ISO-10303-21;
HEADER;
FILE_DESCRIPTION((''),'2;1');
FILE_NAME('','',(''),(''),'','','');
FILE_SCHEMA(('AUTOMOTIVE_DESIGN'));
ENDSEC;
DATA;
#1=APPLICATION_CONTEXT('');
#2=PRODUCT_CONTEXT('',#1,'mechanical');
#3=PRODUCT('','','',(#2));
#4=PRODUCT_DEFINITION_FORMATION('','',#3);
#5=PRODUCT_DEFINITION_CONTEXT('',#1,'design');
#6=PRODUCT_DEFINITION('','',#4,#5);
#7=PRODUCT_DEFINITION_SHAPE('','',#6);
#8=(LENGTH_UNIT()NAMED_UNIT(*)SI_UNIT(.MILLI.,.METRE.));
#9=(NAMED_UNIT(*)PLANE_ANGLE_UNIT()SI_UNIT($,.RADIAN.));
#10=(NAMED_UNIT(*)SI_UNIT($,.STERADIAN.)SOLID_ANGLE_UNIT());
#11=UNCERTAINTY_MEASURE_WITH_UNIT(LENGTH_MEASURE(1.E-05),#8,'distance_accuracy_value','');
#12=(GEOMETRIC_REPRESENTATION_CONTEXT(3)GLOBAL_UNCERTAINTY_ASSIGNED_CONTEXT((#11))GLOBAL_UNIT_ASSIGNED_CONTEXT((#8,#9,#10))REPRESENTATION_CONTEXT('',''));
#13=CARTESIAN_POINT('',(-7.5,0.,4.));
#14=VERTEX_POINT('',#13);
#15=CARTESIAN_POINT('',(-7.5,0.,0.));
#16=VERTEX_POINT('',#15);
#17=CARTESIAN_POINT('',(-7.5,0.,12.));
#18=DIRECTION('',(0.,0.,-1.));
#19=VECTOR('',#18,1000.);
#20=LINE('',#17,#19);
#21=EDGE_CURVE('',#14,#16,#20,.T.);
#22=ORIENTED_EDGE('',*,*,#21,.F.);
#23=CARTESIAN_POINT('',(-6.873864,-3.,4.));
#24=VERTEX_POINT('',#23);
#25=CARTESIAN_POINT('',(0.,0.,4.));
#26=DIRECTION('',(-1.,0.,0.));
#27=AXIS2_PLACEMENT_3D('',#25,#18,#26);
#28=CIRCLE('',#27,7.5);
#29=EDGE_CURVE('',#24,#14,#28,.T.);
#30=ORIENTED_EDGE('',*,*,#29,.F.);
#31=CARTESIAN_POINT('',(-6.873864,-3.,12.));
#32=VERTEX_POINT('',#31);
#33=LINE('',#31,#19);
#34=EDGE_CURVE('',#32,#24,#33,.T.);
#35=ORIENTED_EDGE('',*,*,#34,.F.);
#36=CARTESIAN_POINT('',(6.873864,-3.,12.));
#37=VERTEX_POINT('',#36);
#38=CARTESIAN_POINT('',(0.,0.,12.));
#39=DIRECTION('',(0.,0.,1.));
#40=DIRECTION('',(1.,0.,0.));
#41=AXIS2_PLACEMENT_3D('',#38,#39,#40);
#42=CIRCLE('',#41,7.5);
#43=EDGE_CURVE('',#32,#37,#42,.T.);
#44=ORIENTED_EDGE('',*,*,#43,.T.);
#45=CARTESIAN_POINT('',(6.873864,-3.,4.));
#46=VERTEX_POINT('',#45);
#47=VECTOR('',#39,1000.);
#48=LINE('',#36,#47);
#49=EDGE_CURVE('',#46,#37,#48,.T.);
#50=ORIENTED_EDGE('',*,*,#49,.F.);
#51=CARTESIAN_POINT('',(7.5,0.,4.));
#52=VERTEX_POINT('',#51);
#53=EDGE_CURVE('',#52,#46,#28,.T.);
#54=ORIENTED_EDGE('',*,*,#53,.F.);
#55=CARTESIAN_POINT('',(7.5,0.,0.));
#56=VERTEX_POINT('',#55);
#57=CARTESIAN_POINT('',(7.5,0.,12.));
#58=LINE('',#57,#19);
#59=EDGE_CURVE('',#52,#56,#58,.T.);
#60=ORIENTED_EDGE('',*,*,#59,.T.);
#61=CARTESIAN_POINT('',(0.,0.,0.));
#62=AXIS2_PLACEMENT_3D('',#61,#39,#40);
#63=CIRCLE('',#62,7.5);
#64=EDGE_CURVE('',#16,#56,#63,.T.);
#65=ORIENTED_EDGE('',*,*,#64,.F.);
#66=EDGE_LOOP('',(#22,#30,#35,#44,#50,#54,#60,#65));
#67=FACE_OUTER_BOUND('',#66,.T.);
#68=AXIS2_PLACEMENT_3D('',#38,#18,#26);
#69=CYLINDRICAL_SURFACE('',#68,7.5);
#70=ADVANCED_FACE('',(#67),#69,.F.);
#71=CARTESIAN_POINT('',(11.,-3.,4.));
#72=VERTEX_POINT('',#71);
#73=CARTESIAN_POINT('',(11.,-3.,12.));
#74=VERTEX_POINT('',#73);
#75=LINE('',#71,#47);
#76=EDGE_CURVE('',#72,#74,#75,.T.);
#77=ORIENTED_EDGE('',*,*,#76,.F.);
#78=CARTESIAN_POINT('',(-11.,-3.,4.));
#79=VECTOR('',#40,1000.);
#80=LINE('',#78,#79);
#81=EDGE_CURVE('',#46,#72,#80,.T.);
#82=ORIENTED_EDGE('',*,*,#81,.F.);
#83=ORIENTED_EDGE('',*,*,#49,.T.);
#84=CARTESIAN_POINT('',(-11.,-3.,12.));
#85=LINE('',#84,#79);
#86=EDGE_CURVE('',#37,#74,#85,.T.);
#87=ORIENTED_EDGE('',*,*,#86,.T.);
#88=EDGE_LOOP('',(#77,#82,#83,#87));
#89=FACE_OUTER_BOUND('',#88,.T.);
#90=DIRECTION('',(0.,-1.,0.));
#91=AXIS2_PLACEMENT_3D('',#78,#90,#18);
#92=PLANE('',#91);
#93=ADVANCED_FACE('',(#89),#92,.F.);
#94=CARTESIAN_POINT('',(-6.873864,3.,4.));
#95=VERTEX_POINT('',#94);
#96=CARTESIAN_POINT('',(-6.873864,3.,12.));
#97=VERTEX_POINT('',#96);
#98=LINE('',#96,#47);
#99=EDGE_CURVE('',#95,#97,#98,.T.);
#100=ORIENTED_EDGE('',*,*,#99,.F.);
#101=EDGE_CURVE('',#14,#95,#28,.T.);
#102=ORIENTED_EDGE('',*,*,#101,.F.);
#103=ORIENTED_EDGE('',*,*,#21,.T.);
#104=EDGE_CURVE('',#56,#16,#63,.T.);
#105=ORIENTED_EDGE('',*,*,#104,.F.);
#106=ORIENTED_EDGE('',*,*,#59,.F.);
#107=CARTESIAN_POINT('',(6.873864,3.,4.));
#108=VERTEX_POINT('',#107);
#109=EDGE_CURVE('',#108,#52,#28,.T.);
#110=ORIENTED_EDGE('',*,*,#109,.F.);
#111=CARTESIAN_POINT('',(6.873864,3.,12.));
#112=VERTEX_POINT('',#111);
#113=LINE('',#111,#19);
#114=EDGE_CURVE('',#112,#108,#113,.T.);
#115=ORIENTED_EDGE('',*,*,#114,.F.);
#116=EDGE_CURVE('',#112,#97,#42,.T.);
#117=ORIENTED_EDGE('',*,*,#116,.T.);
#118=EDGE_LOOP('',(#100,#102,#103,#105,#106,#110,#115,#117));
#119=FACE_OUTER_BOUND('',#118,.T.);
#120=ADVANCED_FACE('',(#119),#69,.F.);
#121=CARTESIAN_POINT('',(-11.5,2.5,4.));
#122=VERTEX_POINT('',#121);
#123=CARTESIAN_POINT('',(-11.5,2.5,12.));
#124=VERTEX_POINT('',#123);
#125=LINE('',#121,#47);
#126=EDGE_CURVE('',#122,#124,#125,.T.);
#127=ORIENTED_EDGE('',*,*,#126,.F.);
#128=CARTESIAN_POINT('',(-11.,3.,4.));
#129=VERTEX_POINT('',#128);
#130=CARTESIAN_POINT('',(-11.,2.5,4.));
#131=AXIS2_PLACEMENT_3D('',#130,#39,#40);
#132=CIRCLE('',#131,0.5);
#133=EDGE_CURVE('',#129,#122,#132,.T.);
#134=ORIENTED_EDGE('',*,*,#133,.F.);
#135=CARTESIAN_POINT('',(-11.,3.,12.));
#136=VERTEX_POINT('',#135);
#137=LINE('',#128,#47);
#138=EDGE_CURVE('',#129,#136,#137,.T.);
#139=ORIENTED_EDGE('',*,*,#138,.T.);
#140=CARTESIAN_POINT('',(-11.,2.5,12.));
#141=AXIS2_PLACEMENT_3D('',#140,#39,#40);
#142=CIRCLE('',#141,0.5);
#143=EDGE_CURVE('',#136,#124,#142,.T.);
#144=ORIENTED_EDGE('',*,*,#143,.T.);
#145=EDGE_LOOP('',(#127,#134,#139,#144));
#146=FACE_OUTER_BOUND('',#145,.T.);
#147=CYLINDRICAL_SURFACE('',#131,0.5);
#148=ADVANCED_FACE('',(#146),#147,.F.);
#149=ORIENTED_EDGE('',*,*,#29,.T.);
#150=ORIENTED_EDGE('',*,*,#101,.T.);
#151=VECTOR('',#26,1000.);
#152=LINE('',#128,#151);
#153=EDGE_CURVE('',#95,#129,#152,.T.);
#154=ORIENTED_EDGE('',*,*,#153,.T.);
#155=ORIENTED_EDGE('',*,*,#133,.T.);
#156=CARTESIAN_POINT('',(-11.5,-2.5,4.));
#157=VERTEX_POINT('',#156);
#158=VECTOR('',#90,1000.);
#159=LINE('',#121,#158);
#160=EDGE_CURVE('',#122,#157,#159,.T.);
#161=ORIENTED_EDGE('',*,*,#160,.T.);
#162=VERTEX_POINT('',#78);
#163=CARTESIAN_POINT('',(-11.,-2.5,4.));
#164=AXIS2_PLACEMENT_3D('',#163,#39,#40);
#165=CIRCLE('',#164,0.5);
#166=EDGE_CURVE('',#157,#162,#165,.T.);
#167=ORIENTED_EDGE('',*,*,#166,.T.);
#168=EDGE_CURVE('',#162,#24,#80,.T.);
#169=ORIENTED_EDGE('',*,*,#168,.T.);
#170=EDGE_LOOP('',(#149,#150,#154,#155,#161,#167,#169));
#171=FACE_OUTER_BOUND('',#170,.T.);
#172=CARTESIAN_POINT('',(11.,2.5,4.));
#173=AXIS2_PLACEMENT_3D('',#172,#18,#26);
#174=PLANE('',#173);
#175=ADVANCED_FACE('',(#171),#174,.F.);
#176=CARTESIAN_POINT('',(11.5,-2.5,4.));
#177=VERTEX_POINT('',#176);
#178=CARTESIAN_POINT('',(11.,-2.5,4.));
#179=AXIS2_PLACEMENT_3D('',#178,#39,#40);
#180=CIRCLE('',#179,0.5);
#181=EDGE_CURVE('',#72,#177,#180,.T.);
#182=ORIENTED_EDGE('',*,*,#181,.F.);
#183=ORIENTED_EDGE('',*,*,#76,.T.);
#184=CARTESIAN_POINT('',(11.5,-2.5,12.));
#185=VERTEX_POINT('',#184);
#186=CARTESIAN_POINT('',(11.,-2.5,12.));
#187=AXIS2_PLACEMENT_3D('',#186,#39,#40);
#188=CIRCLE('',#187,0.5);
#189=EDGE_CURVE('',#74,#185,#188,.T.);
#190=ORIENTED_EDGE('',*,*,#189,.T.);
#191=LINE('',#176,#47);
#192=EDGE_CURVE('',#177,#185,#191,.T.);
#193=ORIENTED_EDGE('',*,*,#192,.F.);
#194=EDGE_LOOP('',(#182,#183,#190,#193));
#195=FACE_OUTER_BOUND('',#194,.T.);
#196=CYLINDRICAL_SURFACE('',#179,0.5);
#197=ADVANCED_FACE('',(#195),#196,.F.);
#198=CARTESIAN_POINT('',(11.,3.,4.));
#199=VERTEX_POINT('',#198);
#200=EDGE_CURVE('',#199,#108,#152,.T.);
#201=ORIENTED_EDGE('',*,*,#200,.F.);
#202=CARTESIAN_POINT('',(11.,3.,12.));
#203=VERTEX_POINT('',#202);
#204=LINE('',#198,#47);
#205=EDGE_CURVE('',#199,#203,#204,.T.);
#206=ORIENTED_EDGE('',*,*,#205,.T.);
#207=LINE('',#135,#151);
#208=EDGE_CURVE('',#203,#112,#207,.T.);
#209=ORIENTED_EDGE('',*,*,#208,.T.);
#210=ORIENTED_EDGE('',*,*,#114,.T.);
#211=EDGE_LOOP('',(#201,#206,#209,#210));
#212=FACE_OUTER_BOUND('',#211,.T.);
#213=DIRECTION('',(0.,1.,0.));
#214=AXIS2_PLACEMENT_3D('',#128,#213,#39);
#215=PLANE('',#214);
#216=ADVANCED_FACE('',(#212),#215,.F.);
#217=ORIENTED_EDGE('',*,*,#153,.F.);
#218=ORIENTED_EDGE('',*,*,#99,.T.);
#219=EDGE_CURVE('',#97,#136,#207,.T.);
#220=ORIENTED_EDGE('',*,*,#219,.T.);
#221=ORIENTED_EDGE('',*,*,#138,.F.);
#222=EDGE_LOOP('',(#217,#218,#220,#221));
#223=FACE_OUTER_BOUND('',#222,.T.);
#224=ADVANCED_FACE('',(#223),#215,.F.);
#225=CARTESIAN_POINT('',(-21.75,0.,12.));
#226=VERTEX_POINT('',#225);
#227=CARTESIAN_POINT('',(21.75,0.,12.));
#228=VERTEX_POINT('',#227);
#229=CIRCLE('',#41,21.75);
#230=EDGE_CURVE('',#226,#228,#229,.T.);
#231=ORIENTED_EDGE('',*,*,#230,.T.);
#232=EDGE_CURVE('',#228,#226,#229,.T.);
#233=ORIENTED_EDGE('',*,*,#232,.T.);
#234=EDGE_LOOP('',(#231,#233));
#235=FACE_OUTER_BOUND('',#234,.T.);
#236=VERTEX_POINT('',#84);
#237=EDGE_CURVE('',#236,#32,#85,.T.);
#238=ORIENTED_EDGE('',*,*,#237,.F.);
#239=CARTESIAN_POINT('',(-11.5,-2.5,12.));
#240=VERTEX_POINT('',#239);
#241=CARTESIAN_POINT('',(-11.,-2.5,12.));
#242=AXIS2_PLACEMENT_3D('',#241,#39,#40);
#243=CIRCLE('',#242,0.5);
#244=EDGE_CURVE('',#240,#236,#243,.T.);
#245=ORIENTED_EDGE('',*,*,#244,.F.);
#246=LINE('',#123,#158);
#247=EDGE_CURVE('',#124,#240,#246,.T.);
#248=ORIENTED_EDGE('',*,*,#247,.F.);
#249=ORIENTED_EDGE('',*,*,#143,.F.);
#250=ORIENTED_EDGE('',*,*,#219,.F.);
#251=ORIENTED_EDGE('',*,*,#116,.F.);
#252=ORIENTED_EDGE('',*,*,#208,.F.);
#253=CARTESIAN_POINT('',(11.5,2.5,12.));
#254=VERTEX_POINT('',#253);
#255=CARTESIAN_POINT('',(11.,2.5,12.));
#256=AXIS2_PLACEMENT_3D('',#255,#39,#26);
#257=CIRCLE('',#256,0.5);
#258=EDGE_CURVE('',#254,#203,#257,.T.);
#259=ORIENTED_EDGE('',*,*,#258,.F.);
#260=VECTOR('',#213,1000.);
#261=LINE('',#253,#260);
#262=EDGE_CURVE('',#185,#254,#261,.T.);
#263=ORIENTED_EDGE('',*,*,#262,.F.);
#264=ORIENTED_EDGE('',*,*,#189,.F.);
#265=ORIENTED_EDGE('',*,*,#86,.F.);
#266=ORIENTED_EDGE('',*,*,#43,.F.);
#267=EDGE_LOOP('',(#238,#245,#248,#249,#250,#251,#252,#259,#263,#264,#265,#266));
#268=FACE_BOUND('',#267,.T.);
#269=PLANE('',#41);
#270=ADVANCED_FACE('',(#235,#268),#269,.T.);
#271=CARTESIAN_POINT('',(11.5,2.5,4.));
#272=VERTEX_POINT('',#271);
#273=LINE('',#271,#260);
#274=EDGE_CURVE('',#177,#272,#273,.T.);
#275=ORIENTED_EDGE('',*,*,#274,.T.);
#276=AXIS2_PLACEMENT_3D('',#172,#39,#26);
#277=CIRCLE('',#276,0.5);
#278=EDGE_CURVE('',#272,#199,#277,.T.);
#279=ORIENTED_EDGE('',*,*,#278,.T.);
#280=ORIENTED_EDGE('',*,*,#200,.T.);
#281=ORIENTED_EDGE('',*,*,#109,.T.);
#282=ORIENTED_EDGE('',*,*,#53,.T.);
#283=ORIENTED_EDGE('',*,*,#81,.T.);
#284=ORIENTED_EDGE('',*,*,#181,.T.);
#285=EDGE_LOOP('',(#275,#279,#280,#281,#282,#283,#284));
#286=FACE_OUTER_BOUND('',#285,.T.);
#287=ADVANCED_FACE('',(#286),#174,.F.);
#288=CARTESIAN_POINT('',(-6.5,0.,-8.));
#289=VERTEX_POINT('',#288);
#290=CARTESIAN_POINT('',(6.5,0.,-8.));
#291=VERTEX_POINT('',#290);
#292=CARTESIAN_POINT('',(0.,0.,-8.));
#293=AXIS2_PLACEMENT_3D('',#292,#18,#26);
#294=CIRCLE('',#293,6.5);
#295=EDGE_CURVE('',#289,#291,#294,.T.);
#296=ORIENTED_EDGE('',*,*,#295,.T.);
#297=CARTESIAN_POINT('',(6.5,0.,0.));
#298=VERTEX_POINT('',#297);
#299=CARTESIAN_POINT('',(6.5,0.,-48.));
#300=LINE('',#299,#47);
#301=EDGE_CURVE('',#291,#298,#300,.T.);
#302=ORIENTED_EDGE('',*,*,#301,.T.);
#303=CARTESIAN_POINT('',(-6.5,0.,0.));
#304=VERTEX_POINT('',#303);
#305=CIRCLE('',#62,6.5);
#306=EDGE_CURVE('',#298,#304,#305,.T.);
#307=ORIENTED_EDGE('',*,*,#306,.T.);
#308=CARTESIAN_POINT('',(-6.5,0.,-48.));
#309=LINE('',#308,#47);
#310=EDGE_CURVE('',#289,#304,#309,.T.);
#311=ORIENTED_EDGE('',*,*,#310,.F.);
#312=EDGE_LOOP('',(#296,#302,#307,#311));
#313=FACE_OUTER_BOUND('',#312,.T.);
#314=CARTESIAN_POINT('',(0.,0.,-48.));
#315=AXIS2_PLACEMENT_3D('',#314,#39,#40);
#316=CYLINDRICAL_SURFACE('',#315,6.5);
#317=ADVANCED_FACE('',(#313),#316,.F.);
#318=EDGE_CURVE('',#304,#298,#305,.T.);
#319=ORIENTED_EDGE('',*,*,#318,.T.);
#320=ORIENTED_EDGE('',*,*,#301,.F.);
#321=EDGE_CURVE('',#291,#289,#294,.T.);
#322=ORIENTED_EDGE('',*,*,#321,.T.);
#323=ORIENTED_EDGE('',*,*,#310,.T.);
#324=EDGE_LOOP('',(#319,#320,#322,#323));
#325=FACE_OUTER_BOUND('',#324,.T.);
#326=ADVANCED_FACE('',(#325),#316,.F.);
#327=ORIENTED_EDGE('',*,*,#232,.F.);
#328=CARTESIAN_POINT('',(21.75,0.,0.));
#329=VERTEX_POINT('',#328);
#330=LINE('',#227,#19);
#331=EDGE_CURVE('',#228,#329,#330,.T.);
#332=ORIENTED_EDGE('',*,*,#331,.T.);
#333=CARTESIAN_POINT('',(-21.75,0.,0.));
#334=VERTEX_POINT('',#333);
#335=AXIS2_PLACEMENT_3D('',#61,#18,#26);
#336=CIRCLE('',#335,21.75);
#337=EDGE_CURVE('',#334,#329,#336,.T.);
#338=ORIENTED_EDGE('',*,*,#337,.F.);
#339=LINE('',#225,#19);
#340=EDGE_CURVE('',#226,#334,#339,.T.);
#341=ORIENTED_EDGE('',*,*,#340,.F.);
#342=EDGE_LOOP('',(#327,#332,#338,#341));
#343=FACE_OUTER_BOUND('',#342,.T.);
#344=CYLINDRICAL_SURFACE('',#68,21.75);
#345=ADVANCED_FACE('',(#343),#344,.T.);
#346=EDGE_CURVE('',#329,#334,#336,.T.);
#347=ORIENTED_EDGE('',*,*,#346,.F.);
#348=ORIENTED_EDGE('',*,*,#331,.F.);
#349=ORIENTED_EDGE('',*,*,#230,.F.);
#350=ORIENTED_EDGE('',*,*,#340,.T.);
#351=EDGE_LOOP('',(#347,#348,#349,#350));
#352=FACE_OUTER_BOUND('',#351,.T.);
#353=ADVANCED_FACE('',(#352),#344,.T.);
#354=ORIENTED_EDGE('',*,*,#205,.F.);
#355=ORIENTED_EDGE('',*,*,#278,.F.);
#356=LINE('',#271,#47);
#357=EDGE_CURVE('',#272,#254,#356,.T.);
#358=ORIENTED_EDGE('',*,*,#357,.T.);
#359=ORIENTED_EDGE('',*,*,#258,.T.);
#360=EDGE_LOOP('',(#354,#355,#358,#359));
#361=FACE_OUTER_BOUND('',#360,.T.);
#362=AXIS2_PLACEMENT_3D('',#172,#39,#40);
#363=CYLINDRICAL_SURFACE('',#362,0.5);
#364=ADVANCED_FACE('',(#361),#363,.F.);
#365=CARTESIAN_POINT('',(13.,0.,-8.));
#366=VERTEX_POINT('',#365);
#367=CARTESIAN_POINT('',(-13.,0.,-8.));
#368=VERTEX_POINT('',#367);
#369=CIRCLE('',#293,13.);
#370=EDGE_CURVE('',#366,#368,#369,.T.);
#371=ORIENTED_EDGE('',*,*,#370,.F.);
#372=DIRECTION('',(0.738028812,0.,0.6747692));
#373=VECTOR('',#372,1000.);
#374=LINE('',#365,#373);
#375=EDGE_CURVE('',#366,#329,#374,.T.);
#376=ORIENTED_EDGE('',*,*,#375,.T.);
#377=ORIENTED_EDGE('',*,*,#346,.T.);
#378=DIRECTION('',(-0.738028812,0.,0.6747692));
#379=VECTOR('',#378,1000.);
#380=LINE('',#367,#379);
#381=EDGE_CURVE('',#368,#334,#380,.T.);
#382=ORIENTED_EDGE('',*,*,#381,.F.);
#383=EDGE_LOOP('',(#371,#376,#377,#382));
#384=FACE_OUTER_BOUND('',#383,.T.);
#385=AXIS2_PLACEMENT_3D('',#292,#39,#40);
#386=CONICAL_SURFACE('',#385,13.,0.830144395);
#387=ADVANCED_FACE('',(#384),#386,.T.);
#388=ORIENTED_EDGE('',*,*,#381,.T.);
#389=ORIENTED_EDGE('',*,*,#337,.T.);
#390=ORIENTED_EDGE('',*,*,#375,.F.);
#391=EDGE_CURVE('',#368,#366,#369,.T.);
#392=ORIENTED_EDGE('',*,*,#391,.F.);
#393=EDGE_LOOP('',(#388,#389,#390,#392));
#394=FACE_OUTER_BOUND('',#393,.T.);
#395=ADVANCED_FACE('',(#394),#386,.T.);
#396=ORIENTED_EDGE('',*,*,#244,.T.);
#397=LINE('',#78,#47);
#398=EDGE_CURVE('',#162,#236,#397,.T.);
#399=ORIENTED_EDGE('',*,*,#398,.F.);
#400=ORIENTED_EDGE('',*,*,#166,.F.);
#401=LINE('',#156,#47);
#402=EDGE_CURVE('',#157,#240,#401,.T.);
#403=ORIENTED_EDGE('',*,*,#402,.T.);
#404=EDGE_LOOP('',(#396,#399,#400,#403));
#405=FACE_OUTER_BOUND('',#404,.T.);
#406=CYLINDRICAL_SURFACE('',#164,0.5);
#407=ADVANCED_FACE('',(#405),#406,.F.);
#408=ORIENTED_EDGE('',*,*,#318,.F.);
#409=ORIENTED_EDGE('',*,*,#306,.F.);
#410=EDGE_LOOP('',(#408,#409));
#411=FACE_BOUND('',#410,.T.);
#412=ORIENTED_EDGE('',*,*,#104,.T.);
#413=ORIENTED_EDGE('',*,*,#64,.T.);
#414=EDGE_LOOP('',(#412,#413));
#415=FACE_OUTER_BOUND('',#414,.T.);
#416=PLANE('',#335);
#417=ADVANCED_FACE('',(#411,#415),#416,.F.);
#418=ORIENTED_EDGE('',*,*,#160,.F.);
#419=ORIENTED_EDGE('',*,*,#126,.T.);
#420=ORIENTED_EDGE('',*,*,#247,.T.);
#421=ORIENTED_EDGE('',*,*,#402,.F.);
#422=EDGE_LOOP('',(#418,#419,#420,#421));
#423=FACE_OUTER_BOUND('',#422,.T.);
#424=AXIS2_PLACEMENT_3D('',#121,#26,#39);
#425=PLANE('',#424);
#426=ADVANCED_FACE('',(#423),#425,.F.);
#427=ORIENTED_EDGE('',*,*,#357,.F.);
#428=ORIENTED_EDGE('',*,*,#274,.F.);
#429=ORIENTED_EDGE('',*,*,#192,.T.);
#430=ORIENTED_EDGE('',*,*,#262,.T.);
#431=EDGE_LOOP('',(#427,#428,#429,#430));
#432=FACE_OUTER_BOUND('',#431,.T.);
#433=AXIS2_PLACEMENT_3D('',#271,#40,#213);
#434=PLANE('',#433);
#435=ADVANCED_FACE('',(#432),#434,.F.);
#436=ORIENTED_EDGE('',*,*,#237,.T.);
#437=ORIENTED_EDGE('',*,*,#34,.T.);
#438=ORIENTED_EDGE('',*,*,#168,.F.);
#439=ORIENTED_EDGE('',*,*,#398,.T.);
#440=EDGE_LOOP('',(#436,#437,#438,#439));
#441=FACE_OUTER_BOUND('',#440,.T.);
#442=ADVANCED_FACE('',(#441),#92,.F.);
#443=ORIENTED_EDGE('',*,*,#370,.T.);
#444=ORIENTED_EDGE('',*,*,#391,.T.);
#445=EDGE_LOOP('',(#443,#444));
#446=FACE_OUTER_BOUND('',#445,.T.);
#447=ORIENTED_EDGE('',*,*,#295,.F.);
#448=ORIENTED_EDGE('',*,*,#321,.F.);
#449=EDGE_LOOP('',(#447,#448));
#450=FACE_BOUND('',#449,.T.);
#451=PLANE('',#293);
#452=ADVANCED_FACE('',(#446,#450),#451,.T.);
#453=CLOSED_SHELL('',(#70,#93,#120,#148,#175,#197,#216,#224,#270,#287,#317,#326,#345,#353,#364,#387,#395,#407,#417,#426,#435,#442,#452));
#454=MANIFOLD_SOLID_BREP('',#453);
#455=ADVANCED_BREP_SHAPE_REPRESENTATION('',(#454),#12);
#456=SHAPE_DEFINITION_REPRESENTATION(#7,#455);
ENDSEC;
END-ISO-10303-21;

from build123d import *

# Parameters (mm, degrees)
SKETCH_1_R          = 21.75
SKETCH_1_R_2        = 7.5
EXTRUDE_1_DEPTH     = 12
CUT_EXTRUDE_1_DEPTH = 8
SKETCH_4_R          = 21.75
SKETCH_5_R          = 13
SKETCH_6_R          = 6.5
CUT_EXTRUDE_3_DEPTH = 48


with BuildPart() as part:
    # 草图1 → 凸台-拉伸1 (new body)
    with BuildSketch(Plane.XY):
        Circle(SKETCH_1_R)
        Circle(SKETCH_1_R_2, mode=Mode.SUBTRACT)
    extrude(amount=EXTRUDE_1_DEPTH)

    # 草图2 → 切除-拉伸1 (cut)
    with BuildSketch(Plane.XY.offset(12)):
        with BuildLine():
            Line((-11, 3), (11, 3))
            ThreePointArc((11, 3), (11.353553391, 2.853553391), (11.5, 2.5))
            Line((11.5, 2.5), (11.5, -2.5))
            ThreePointArc((11.5, -2.5), (11.353553391, -2.853553391), (11, -3))
            Line((11, -3), (-11, -3))
            ThreePointArc((-11, -3), (-11.353553391, -2.853553391), (-11.5, -2.5))
            Line((-11.5, -2.5), (-11.5, 2.5))
            ThreePointArc((-11.5, 2.5), (-11.353553391, 2.853553391), (-11, 3))
        make_face()
    extrude(amount=-CUT_EXTRUDE_1_DEPTH, mode=Mode.SUBTRACT)

    # 草图4 → 放样2 section 0
    with BuildSketch(Plane(origin=(0, 0, 0), x_dir=(-1, 0, 0), z_dir=(0, 0, -1))):
        Circle(SKETCH_4_R)
    # 草图5 → 放样2 section 1
    with BuildSketch(Plane(origin=(0, 0, -8), x_dir=(-1, 0, 0), z_dir=(0, 0, -1))):
        Circle(SKETCH_5_R)
    loft()

    # 草图6 → 切除-拉伸3 (cut)
    with BuildSketch(Plane.XY):
        Circle(SKETCH_6_R)
    extrude(amount=-CUT_EXTRUDE_3_DEPTH, mode=Mode.SUBTRACT)


solid = part.part
